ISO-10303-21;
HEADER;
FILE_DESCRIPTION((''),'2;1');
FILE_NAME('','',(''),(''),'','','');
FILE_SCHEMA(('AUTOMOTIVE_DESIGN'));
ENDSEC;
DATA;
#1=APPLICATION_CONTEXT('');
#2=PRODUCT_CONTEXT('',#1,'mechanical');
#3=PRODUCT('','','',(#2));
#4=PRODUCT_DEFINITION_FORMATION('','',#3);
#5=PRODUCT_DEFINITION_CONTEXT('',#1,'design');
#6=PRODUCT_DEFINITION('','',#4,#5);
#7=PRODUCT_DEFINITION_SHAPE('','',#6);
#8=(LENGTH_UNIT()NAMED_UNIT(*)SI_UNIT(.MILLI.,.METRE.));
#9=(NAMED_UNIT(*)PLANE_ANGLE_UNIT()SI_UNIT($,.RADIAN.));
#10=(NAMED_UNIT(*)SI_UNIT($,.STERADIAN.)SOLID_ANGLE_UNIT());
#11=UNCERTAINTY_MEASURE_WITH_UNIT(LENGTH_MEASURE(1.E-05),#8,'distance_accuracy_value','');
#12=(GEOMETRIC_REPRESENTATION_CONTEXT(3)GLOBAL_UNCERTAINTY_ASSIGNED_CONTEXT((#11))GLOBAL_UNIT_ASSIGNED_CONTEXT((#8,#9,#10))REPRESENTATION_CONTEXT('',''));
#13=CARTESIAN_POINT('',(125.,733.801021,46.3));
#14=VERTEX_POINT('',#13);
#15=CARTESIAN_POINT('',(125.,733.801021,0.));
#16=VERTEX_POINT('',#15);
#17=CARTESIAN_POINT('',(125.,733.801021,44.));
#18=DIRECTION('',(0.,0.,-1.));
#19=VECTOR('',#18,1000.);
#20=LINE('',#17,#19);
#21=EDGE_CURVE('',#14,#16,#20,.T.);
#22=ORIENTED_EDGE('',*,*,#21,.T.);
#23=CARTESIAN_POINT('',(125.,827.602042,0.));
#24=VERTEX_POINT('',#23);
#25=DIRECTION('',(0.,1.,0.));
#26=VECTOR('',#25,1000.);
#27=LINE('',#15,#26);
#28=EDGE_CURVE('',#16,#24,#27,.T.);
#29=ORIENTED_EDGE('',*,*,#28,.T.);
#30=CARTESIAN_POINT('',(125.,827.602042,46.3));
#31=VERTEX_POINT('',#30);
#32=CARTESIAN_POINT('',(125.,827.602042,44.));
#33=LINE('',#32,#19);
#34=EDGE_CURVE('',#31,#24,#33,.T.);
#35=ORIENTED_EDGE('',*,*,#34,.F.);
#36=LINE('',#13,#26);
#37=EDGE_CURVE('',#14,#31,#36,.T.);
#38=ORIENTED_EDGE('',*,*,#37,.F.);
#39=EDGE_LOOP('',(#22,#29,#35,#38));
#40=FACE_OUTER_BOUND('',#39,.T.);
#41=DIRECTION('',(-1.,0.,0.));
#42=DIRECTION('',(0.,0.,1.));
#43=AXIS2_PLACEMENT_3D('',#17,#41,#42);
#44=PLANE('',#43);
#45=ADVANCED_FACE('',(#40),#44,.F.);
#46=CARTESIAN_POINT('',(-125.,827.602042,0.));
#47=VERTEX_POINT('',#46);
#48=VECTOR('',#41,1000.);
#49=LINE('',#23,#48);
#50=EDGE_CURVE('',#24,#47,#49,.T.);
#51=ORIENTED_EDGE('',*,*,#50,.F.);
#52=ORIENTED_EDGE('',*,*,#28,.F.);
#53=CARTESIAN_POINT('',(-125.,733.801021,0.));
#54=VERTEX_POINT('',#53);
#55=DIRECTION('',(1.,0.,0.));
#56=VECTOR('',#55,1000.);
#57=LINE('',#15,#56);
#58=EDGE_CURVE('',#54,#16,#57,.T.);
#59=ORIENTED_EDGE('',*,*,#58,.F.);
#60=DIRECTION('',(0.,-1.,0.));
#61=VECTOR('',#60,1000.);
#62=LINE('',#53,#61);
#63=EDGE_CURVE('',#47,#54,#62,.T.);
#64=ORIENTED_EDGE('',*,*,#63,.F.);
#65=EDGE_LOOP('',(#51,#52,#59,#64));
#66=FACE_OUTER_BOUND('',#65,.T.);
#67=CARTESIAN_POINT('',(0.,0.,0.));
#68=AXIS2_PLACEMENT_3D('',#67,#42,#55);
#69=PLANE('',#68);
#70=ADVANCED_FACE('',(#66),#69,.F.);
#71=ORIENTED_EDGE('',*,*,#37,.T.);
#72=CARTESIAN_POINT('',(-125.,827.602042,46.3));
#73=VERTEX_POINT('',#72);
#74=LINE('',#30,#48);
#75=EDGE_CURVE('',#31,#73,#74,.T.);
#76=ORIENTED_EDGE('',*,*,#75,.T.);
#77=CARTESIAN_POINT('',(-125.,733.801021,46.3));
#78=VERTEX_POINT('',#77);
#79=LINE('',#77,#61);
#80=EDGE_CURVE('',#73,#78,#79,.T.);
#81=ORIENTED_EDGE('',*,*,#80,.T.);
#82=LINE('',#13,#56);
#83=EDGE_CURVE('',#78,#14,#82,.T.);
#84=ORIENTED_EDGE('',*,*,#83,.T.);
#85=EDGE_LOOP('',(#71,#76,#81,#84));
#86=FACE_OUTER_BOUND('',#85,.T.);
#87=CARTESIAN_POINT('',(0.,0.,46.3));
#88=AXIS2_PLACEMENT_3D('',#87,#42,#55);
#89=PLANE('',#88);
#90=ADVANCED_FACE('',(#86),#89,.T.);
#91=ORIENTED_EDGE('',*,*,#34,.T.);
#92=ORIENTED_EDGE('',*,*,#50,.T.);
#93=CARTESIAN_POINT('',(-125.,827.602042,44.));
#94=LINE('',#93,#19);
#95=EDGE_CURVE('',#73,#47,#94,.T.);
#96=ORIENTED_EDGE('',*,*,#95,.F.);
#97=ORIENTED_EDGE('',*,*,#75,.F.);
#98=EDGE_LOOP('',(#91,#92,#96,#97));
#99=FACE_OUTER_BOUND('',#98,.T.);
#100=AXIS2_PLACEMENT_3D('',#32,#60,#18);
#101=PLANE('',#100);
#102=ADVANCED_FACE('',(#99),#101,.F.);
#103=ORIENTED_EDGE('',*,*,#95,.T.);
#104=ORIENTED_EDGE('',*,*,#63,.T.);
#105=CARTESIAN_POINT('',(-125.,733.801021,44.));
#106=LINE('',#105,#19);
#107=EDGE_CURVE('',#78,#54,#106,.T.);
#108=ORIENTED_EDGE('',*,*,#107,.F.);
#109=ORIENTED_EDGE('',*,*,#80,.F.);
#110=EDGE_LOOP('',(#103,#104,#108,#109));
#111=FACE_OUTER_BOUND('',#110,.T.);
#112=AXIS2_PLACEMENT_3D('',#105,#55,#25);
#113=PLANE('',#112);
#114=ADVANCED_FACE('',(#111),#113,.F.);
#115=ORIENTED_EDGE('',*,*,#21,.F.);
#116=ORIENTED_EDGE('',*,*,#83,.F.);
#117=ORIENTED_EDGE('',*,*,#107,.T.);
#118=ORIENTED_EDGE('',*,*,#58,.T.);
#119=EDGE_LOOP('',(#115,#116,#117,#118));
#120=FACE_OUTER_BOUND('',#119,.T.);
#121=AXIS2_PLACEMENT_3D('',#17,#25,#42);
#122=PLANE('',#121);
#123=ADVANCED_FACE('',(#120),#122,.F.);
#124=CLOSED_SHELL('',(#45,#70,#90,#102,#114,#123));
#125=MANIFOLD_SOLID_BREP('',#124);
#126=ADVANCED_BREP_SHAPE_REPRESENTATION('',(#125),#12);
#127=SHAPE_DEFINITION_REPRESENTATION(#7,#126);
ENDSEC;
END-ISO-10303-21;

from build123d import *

# Parameters (mm, degrees)
SKETCH2_W           = 250
SKETCH2_H           = 93.801020924
BOSS_EXTRUDE1_DEPTH = 44
MOVE_FACE1_BY       = 2.3


with BuildPart() as part:
    # Sketch2 → Boss-Extrude1 (new body)
    with BuildSketch(Plane.XY):
        with Locations((0, 780.701531386)):
            Rectangle(SKETCH2_W, SKETCH2_H)
    extrude(amount=BOSS_EXTRUDE1_DEPTH)

    # Move Face1: a face moved outward by 2.3
    extrude(part.faces().sort_by_distance((0, 780.701531386, 44))[0], amount=MOVE_FACE1_BY, dir=(0, 0, 1))


solid = part.part
